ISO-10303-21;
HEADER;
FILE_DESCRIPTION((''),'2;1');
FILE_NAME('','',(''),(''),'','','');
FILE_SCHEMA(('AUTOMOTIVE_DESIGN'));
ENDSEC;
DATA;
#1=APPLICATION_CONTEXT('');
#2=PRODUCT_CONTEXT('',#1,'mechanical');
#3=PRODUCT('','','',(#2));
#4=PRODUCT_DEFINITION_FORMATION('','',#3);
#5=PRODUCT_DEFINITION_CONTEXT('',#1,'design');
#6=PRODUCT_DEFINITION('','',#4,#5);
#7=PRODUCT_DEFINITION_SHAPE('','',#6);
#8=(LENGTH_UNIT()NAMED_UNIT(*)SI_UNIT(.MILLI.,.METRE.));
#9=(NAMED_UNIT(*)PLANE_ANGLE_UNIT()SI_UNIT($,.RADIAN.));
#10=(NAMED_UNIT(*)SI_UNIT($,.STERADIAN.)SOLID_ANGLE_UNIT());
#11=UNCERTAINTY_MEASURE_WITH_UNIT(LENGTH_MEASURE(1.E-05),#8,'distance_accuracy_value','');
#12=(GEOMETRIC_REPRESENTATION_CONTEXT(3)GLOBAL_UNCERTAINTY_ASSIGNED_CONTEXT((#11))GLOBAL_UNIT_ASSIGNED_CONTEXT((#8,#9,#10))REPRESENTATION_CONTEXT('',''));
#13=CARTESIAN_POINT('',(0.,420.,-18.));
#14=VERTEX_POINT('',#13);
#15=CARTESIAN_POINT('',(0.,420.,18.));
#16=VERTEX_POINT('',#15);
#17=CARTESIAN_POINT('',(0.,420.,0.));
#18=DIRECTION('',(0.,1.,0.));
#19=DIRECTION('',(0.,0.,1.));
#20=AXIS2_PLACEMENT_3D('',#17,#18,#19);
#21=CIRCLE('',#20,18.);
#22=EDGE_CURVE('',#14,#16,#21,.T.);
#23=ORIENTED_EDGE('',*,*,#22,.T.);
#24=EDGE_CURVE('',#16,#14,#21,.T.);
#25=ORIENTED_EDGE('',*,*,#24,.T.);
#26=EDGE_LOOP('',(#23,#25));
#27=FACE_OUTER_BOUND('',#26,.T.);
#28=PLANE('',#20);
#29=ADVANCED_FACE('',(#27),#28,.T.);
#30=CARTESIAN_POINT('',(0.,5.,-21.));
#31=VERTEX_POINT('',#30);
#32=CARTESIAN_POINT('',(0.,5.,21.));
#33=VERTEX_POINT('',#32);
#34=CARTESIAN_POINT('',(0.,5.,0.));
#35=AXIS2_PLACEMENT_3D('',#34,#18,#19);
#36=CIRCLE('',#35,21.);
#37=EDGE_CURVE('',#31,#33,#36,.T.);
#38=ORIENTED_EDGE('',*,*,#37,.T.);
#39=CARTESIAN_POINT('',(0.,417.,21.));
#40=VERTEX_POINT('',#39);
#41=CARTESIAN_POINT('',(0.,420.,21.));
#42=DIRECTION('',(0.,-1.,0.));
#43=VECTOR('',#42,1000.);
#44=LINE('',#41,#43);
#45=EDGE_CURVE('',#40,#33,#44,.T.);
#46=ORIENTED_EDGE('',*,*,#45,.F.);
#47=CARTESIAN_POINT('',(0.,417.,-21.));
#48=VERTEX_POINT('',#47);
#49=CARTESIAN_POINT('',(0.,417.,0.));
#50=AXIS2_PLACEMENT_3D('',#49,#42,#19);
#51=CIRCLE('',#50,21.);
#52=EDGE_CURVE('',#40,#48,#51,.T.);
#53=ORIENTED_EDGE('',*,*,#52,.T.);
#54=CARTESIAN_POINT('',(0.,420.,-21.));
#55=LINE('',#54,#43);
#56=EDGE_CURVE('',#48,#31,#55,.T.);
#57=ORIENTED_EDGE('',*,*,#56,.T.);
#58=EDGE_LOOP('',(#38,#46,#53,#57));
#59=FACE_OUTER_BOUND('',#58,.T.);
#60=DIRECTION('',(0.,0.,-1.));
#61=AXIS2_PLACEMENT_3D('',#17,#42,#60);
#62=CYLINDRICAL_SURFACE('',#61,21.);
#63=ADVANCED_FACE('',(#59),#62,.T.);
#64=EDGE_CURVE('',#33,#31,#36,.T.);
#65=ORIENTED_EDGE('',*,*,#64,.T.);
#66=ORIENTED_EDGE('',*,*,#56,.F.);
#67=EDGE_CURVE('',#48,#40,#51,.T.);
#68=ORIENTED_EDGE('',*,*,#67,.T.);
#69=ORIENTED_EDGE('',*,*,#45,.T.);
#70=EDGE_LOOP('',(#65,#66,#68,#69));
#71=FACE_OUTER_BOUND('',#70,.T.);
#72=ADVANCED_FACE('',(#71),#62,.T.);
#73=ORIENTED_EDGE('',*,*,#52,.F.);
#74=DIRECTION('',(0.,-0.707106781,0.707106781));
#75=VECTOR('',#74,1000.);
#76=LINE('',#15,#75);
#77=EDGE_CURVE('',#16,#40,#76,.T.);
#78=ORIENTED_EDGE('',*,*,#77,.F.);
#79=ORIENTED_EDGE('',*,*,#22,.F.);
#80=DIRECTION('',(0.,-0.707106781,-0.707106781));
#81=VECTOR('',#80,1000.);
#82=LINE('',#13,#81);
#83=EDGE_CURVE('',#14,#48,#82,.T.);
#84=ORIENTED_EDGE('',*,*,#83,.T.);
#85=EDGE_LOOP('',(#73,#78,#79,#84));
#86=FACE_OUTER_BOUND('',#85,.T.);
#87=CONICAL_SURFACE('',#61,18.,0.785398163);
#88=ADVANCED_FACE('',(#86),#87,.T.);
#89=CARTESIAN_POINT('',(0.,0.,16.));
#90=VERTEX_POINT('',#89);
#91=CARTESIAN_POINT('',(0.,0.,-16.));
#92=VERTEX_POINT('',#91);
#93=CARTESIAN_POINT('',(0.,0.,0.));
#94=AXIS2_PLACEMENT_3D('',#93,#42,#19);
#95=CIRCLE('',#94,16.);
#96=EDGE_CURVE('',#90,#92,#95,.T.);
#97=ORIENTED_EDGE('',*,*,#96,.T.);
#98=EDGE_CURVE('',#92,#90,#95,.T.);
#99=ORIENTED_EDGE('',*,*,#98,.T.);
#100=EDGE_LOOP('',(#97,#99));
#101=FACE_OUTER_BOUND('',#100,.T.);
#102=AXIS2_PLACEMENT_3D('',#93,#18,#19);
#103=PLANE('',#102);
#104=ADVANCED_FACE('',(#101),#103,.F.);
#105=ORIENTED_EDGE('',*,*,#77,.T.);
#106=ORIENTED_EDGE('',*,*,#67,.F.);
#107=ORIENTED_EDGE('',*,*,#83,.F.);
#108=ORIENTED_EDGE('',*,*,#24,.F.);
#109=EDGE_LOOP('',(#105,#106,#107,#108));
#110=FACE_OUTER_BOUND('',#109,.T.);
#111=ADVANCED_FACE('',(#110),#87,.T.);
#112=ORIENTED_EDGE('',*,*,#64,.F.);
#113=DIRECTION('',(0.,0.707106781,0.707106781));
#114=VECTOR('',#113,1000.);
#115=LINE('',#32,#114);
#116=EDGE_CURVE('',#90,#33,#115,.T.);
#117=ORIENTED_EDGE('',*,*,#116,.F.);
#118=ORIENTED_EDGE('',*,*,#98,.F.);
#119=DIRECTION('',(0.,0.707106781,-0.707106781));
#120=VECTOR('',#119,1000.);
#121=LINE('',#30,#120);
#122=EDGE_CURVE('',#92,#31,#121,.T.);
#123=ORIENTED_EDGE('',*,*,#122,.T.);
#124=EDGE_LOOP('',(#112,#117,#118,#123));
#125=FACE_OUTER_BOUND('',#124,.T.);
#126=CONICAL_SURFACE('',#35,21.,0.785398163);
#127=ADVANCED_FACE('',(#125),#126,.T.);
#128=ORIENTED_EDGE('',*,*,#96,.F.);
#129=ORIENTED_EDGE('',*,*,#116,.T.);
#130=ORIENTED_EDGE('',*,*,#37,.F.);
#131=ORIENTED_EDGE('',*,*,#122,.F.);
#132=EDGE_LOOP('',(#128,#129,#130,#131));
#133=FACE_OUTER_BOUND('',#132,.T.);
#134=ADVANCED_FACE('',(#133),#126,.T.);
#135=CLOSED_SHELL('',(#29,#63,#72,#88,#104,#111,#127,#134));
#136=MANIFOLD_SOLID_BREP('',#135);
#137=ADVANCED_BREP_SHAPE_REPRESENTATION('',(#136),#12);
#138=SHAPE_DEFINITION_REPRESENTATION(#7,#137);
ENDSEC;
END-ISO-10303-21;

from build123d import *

# Parameters (mm, degrees)
SKETCH2_R           = 21
BOSS_EXTRUDE1_DEPTH = 420
CHAMFER1_SIZE       = 5
CHAMFER2_SIZE       = 3


with BuildPart() as part:
    # Sketch2 → Boss-Extrude1 (new body)
    with BuildSketch(Plane(origin=(0, 0, 0), x_dir=(1, 0, 0), z_dir=(0, 1, 0))):
        with Locations(Location((0, 0, 0), (0, 0, 270))):
            Circle(SKETCH2_R)
    extrude(amount=BOSS_EXTRUDE1_DEPTH)

    # Chamfer1
    chamfer1_edges = [part.edges().sort_by_distance(p)[0] for p in [
        (0, 0, -21),
    ]]
    chamfer(chamfer1_edges, length=CHAMFER1_SIZE)

    # Chamfer2
    chamfer2_edges = [part.edges().sort_by_distance(p)[0] for p in [
        (0, 420, -21),
    ]]
    chamfer(chamfer2_edges, length=CHAMFER2_SIZE)


solid = part.part
